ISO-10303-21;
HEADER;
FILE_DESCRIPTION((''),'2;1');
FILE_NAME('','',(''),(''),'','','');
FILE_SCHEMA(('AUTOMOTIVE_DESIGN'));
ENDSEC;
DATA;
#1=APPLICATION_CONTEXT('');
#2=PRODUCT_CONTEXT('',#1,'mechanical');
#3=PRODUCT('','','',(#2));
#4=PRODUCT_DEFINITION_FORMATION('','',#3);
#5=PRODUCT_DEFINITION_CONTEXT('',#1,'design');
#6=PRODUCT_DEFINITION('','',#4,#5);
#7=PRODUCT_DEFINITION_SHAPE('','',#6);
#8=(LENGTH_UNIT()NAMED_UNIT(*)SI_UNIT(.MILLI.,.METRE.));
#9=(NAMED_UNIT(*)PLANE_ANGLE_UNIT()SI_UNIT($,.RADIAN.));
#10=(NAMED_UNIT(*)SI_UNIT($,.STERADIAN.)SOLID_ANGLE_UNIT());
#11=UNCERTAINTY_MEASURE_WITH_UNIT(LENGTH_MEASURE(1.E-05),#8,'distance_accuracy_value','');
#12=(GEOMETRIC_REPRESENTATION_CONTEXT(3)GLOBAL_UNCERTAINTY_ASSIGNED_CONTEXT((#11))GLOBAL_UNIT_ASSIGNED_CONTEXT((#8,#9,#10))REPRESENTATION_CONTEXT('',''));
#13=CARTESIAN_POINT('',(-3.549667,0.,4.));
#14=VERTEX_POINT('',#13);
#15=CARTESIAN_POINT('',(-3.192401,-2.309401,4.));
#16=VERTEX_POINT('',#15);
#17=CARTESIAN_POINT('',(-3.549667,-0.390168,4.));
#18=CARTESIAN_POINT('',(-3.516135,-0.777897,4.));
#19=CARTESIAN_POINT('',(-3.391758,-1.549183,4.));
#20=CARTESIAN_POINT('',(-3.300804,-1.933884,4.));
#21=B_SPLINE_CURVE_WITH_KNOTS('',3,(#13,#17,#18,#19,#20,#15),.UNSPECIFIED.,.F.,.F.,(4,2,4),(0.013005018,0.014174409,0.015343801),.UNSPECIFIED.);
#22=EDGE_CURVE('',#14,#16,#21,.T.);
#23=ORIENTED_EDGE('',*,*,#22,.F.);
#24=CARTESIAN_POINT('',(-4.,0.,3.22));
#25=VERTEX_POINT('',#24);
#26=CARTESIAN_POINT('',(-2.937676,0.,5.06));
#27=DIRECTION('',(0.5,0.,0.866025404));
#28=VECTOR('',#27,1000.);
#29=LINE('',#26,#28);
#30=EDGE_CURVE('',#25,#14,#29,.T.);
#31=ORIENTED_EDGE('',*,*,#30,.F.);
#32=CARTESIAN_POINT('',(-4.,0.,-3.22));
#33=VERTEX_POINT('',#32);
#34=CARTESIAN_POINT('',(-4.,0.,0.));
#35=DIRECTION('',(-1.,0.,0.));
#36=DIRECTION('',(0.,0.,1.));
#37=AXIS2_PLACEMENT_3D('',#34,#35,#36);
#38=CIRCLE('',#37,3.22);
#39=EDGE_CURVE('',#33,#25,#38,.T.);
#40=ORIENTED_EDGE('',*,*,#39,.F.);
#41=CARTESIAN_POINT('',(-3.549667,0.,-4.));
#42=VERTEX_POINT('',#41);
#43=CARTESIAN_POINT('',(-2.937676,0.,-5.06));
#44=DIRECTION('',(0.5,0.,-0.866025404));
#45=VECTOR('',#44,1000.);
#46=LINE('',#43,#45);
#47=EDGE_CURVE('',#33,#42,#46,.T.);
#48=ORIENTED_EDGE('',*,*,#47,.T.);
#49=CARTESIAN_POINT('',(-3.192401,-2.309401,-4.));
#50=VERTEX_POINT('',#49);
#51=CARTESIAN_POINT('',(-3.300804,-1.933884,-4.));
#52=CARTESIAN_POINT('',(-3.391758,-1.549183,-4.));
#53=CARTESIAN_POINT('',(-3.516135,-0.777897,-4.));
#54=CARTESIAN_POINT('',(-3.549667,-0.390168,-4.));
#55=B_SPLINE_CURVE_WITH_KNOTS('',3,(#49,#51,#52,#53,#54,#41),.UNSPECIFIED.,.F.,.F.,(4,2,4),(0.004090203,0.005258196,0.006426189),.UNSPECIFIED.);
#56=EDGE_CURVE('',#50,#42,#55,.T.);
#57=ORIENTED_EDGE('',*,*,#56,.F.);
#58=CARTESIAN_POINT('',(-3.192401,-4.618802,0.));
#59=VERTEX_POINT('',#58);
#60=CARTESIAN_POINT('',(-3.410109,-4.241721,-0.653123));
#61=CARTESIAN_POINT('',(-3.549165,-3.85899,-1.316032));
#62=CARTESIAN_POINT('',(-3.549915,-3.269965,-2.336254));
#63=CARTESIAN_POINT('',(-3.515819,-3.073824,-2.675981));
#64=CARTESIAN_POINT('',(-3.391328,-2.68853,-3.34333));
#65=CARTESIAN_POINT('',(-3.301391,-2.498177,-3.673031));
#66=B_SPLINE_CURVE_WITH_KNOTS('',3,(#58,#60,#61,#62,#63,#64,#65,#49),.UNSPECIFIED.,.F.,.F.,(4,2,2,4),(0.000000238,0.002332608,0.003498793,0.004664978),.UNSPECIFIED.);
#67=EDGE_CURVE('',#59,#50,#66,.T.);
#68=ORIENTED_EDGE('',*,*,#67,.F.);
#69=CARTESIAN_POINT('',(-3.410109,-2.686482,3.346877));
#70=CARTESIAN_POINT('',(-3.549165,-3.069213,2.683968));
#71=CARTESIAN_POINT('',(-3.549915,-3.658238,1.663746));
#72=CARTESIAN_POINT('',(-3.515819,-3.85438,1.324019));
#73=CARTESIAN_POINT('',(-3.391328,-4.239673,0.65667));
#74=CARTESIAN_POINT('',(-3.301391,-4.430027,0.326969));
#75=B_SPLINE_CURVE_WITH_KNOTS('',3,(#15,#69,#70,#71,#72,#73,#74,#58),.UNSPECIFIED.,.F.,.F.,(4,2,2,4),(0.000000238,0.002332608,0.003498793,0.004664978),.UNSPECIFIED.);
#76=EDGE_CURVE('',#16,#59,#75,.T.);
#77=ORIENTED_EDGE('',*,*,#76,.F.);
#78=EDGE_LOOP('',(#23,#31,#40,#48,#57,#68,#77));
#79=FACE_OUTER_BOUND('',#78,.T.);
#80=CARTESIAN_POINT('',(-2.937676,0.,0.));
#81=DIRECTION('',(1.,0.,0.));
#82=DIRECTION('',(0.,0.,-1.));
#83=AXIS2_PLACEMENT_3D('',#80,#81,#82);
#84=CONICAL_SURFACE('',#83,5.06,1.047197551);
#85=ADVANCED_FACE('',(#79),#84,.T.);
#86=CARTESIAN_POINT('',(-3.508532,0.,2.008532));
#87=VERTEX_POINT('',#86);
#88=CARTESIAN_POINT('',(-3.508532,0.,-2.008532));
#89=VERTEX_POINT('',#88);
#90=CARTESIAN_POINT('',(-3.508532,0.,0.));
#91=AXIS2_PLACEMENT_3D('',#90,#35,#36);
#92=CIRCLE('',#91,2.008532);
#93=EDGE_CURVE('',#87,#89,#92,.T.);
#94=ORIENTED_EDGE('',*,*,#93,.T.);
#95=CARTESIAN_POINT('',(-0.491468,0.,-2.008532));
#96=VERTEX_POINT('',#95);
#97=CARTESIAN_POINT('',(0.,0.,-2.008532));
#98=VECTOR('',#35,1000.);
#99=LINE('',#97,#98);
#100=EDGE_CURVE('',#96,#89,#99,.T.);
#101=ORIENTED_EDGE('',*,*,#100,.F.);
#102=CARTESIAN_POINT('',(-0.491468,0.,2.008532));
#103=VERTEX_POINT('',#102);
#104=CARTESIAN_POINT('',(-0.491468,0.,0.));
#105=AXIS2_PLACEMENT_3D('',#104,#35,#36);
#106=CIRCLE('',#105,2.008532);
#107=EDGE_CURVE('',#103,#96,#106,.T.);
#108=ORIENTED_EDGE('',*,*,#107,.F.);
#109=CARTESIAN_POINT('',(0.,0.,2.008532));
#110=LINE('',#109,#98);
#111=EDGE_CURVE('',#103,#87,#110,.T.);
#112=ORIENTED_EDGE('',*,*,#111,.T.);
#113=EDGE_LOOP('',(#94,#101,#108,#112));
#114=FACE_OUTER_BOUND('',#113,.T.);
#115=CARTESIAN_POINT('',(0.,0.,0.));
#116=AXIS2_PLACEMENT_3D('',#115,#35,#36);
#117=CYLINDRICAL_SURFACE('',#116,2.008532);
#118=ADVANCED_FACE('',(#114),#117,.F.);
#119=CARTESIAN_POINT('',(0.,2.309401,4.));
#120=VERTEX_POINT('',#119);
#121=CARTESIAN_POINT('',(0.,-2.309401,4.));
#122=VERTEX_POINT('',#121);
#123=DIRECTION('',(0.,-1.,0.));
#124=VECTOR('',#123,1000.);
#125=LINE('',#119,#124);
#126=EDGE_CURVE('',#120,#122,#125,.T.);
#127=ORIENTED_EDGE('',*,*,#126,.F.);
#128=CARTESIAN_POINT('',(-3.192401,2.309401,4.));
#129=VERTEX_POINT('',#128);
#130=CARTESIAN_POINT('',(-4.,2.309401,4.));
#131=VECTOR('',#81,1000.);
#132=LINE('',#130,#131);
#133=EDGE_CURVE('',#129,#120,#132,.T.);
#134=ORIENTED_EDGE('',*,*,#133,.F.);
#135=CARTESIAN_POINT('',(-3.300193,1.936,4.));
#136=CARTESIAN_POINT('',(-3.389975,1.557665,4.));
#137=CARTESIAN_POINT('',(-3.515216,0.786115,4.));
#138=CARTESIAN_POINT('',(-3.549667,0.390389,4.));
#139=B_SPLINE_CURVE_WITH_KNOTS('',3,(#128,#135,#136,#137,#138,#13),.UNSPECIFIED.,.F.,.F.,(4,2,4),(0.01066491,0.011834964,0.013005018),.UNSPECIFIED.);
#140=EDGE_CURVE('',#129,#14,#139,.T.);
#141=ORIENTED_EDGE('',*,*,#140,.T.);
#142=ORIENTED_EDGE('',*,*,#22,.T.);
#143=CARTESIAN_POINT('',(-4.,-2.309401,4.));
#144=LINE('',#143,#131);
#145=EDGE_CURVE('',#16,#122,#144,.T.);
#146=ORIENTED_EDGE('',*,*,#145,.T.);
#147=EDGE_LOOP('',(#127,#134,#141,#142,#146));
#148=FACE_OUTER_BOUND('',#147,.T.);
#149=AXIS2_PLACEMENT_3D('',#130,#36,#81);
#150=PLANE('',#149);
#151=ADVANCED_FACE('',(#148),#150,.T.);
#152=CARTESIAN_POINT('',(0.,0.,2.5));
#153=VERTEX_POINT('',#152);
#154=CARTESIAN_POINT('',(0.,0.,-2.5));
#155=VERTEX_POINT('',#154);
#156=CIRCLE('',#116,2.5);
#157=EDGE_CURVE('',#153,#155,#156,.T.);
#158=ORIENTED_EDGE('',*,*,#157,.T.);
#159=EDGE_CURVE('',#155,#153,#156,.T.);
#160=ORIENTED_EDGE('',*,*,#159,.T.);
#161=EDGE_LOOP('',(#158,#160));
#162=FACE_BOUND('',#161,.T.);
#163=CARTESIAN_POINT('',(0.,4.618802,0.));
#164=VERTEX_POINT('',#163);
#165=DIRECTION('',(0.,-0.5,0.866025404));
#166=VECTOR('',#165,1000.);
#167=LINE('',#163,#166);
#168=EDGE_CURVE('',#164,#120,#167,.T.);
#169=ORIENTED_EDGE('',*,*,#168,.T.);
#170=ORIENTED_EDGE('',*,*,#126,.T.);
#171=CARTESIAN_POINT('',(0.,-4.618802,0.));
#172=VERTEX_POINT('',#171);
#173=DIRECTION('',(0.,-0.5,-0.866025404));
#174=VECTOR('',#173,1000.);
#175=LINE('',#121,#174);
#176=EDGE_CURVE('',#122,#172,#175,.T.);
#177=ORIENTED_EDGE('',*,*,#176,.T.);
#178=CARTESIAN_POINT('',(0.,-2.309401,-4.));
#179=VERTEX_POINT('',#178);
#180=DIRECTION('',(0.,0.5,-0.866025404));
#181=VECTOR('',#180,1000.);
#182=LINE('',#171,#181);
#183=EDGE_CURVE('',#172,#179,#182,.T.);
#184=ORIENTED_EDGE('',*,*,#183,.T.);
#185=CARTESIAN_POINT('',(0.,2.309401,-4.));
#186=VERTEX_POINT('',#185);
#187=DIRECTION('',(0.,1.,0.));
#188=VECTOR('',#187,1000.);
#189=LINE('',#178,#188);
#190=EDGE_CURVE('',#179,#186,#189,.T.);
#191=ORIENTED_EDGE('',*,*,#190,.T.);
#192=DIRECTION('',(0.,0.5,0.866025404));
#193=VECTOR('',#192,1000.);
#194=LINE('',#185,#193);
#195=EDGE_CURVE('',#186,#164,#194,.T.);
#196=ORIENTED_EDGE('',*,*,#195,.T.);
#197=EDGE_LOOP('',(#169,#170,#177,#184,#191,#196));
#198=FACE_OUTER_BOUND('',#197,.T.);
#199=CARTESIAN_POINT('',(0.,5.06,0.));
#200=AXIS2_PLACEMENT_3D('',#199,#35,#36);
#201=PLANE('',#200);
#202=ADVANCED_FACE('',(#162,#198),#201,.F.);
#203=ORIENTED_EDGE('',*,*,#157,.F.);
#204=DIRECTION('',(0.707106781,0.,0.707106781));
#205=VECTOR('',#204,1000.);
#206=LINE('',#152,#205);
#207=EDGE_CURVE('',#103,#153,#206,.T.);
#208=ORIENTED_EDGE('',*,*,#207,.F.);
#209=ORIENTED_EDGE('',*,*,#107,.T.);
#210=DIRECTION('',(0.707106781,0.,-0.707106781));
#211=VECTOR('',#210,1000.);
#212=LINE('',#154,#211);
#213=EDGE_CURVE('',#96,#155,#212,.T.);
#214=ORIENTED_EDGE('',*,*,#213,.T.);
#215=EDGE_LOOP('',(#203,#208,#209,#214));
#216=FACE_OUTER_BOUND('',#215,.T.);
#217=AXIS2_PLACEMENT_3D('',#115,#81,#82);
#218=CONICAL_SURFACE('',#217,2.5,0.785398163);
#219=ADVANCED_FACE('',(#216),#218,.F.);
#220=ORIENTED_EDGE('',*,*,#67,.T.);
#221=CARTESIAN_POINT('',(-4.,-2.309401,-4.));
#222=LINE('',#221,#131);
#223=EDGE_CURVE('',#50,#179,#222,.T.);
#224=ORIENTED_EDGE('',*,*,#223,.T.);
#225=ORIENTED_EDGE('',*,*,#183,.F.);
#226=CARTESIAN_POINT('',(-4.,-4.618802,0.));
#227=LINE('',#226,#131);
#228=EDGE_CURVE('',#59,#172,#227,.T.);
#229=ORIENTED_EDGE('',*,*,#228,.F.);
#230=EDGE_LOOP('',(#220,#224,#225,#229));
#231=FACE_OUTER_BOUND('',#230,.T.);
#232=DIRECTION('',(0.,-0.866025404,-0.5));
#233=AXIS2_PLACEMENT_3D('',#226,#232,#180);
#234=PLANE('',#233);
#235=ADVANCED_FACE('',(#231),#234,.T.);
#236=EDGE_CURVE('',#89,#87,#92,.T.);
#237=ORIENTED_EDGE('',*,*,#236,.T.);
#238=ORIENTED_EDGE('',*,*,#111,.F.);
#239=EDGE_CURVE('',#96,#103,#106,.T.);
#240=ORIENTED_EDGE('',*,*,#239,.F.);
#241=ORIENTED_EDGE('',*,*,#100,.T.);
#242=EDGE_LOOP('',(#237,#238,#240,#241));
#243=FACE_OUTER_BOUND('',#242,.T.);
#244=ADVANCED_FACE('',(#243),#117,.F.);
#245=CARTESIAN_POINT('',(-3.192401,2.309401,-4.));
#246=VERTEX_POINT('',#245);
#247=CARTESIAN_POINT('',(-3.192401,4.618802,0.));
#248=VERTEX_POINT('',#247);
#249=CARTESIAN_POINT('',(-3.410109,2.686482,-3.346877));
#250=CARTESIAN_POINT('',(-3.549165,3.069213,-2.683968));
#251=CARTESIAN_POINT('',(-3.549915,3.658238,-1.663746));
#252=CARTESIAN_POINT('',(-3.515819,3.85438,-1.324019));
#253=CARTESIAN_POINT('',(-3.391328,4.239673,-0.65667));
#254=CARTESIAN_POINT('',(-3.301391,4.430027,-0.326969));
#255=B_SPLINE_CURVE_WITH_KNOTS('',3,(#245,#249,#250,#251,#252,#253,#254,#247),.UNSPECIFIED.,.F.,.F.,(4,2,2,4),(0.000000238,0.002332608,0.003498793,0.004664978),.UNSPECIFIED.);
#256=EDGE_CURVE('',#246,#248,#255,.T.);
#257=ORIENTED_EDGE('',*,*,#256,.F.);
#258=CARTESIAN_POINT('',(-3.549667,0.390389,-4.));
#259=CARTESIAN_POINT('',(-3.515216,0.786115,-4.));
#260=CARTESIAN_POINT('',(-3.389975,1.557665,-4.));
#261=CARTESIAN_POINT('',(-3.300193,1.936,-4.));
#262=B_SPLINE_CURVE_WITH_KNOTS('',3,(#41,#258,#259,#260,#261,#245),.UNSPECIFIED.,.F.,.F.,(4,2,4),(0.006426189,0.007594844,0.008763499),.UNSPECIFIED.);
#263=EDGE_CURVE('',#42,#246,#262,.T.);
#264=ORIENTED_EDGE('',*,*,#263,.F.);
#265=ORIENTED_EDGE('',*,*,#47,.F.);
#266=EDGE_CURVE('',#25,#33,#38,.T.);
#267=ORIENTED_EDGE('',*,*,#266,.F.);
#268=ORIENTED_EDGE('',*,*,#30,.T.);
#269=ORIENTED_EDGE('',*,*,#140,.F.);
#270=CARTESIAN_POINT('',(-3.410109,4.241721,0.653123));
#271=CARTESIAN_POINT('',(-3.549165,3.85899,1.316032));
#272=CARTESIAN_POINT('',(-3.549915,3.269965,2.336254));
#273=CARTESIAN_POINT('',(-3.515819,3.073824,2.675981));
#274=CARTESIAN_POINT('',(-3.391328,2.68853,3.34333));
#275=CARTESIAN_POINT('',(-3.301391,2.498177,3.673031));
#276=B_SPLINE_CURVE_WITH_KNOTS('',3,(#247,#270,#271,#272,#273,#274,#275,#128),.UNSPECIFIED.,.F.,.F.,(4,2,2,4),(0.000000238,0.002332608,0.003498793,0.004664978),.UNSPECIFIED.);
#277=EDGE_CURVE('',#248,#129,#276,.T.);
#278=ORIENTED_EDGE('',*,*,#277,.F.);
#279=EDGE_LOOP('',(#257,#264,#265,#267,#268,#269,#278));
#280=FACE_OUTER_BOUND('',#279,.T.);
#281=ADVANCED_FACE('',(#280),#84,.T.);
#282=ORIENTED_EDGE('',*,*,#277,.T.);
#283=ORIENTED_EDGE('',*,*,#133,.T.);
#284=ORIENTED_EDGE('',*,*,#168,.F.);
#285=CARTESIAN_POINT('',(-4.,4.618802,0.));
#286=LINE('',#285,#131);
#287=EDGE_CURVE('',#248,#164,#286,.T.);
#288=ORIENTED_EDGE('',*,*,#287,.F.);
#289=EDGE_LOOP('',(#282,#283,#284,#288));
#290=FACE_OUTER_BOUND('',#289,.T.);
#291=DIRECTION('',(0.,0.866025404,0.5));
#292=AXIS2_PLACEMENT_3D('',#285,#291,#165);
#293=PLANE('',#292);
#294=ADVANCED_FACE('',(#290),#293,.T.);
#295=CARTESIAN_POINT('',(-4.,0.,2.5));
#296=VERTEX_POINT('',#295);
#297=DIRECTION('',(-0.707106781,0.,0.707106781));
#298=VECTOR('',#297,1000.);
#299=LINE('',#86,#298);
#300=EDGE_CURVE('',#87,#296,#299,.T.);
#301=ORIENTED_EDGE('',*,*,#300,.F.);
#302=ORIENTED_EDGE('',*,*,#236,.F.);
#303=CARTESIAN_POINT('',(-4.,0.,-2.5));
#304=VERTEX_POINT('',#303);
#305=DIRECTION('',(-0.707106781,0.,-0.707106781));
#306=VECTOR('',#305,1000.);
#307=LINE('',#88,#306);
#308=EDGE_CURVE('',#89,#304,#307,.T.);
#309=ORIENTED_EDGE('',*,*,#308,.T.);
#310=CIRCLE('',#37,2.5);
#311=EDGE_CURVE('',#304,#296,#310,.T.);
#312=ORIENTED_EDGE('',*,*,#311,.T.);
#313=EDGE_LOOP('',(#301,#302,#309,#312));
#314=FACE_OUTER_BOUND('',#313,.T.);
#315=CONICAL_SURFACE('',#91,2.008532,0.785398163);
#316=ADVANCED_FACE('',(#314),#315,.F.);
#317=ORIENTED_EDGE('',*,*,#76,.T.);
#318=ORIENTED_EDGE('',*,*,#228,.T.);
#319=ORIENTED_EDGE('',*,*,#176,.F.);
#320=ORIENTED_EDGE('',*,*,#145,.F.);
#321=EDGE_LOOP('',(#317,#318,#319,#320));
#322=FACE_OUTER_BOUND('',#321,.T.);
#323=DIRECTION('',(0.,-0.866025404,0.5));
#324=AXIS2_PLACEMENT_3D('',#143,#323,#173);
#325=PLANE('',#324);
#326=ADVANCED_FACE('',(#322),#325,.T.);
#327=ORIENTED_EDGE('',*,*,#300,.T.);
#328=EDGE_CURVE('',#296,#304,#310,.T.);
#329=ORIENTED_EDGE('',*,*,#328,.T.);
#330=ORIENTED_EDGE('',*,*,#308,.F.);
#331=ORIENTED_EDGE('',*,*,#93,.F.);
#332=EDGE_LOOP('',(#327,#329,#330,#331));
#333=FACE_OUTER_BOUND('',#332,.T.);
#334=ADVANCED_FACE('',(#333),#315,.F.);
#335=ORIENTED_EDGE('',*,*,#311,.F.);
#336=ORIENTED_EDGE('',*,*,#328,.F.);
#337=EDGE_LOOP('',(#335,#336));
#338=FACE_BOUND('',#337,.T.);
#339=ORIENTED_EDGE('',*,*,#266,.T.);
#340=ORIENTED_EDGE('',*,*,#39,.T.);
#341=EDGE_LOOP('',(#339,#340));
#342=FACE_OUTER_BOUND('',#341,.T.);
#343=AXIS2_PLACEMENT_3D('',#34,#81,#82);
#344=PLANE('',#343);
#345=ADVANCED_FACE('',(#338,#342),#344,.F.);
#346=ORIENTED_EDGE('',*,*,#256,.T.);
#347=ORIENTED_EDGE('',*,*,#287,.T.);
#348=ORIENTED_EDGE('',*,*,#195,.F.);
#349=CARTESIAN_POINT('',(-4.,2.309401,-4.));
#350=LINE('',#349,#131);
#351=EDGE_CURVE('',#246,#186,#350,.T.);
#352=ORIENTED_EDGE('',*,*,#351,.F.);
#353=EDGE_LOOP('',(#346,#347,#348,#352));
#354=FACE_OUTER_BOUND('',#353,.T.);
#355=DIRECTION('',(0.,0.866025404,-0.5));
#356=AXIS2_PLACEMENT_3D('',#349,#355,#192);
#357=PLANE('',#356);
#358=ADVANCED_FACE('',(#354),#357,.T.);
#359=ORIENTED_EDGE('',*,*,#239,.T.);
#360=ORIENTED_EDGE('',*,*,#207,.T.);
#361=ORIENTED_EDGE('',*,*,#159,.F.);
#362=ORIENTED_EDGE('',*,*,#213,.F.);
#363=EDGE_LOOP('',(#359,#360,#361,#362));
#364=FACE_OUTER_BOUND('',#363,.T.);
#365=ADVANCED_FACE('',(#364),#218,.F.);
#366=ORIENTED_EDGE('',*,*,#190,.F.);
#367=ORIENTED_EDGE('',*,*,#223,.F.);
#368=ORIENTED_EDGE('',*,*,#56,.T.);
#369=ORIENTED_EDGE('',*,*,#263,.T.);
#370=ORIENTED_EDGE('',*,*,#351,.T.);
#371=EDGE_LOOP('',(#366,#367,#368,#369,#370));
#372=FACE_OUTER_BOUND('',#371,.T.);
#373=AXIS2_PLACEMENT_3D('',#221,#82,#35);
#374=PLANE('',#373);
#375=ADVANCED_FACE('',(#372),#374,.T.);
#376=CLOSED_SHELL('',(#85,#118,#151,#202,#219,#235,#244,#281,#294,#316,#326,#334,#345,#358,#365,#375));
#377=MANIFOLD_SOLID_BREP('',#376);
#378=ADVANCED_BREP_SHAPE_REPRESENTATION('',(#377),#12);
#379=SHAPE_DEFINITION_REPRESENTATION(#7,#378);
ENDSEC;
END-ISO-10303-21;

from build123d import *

# Parameters (mm, degrees)
SKETCH3_W          = 16
SKETCH3_H          = 16
CUT_EXTRUDE1_DEPTH = 4


with BuildPart() as part:
    # Sketch1 → Revolve1 (revolve)
    with BuildSketch(Plane.XY, mode=Mode.PRIVATE) as revolve1_sk:
        Polygon((-4, 0), (-4, 3.22), (-2.937675505, 5.06), (0, 5.06), (0, 0), align=None)
    revolve(revolve1_sk.sketch.rotate(Axis((0, 0, 0), (-1, 0, 0)), 270), axis=Axis((0, 0, 0), (-1, 0, 0)))

    # Sketch2 → Cut-Revolve1 (revolve, cut)
    with BuildSketch(Plane.XY, mode=Mode.PRIVATE) as cut_revolve1_sk:
        Polygon((-4, 0), (-4, 2.5), (-3.508532, 2.008532), (-0.491468, 2.008532), (0, 2.5), (0, 0), align=None)
    revolve(cut_revolve1_sk.sketch.rotate(Axis((0, 0, 0), (-1, 0, 0)), 270), axis=Axis((0, 0, 0), (-1, 0, 0)), mode=Mode.SUBTRACT)

    # Sketch3 → Cut-Extrude1 (cut)
    with BuildSketch(Plane(origin=(0, 0, 0), x_dir=(0, 0, -1), z_dir=(1, 0, 0))):
        Rectangle(SKETCH3_W, SKETCH3_H)
        Polygon((-4, 2.309401077), (-4, -2.309401077), (0, -4.618802154), (4, -2.309401077), (4, 2.309401077), (0, 4.618802154), align=None, mode=Mode.SUBTRACT)
    extrude(amount=-CUT_EXTRUDE1_DEPTH, mode=Mode.SUBTRACT)


solid = part.part
